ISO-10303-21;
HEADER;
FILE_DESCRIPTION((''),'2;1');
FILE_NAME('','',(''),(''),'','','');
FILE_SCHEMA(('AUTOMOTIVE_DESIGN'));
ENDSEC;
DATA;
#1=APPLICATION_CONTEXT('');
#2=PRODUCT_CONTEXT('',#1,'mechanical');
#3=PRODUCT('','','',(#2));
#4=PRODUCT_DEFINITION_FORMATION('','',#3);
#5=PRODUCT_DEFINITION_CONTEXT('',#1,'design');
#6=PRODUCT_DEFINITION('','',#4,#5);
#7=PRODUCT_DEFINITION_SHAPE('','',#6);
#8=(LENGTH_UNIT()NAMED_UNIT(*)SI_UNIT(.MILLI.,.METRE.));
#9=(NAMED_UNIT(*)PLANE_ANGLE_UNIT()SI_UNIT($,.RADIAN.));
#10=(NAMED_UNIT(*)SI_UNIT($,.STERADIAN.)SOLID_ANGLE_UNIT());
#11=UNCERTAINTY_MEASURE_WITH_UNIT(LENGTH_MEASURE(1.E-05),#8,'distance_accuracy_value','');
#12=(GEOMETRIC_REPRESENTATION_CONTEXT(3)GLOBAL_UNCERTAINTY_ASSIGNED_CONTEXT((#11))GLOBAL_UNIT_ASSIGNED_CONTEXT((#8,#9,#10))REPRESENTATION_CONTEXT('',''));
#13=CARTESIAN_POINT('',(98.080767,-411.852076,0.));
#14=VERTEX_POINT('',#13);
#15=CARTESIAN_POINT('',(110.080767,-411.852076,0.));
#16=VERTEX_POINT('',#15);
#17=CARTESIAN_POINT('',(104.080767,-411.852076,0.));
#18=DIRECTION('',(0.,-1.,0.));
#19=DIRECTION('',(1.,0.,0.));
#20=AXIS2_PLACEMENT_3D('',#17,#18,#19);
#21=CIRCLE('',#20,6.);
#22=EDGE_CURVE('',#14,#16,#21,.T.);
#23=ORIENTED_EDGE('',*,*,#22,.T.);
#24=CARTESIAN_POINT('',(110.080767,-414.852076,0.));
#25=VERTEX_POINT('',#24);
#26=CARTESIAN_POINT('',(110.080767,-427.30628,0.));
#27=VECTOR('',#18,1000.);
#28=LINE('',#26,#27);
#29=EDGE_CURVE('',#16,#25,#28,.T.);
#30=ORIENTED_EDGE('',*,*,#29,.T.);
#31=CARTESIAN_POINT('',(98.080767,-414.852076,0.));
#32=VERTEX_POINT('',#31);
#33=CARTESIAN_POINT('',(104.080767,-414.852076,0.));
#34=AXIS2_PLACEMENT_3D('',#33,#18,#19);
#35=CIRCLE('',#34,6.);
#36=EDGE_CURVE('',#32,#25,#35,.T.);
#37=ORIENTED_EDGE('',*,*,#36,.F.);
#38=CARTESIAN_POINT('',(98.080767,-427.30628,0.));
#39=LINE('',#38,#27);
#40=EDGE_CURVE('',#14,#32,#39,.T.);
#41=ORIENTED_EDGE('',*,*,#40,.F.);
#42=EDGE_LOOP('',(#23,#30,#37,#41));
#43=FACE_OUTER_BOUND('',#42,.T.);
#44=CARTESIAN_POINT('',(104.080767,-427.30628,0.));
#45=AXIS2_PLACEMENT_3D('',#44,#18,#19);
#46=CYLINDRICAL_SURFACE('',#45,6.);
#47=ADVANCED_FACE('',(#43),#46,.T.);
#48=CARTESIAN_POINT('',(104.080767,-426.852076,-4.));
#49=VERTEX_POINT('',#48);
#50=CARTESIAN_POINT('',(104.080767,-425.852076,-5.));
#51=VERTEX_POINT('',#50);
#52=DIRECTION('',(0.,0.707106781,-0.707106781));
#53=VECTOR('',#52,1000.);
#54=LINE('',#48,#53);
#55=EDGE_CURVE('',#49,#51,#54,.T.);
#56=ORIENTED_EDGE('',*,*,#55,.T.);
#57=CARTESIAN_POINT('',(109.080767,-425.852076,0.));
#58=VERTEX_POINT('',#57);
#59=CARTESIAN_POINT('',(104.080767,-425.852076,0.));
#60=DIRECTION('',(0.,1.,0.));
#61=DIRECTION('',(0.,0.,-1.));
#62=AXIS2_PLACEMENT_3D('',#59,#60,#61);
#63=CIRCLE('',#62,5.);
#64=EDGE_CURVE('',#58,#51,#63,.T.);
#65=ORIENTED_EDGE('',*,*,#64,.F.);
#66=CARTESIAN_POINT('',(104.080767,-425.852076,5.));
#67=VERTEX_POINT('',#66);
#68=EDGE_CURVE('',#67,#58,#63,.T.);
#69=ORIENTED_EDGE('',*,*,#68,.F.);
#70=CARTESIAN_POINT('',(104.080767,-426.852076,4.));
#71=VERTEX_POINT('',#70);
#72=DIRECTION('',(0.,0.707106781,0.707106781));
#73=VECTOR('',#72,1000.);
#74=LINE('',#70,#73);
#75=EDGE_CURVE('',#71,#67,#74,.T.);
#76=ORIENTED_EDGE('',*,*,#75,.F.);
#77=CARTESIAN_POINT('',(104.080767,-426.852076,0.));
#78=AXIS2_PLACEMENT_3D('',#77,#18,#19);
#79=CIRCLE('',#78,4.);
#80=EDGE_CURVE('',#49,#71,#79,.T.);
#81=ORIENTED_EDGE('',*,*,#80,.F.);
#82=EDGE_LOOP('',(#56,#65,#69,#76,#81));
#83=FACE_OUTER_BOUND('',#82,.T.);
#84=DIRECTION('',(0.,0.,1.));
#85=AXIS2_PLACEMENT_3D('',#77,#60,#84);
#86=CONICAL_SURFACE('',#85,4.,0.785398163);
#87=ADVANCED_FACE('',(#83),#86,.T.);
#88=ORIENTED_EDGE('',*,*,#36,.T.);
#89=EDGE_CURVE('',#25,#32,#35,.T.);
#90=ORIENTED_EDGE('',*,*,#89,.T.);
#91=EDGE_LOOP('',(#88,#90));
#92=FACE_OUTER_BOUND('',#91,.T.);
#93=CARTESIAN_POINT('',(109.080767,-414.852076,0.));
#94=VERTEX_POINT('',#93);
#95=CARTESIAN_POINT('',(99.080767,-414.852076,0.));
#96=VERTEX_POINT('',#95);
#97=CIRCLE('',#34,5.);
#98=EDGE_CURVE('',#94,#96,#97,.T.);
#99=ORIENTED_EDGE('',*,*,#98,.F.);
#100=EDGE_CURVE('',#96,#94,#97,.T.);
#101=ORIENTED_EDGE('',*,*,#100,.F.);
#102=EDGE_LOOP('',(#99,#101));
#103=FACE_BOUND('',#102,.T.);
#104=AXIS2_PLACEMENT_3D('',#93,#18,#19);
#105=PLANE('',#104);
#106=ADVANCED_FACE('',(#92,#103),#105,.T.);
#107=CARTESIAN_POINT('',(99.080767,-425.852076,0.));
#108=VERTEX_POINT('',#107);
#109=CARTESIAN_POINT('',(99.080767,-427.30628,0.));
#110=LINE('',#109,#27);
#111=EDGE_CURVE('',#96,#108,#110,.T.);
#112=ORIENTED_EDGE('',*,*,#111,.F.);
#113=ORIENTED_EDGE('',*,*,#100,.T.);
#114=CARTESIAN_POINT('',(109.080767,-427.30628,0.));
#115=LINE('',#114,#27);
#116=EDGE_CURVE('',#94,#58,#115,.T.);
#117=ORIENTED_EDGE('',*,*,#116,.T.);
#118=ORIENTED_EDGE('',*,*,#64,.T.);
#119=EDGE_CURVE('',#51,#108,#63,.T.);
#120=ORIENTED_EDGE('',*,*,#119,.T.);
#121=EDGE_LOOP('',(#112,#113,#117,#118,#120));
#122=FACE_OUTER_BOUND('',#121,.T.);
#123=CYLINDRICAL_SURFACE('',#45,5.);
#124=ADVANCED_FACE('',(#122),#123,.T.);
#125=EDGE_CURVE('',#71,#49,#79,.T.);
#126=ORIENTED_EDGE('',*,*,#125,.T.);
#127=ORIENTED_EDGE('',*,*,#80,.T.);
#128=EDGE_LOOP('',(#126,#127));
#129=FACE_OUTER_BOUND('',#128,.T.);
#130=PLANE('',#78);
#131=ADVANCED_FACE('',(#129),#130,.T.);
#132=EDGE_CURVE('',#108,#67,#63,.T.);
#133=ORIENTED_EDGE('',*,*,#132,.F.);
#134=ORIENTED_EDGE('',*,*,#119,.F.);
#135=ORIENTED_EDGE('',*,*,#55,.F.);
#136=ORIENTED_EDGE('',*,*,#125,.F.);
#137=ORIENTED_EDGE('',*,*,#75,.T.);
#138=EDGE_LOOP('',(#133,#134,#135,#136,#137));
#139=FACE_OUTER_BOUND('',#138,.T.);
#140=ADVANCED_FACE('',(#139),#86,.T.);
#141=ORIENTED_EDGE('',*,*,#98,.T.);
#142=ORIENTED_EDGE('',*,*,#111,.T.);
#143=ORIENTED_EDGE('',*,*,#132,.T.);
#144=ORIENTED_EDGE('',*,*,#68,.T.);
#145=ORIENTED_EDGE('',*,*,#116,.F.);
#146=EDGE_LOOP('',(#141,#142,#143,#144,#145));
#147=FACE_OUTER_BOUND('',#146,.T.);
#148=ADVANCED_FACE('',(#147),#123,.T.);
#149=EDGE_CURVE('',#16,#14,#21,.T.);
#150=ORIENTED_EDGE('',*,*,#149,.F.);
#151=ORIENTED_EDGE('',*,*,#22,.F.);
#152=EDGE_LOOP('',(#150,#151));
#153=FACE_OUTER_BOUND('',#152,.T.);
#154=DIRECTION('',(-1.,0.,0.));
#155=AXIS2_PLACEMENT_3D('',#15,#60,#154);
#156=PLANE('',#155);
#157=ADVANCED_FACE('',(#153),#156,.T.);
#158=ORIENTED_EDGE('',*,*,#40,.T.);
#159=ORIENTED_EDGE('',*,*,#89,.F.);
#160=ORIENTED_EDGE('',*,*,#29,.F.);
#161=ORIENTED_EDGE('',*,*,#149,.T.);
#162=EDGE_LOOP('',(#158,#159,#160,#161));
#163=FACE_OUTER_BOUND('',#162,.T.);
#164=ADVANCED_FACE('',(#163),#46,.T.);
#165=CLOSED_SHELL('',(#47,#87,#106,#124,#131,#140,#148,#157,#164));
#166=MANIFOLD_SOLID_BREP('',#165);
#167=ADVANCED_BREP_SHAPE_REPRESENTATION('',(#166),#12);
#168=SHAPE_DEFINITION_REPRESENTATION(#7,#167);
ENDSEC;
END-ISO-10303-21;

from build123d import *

# Parameters (mm, degrees)
CHAMFER1_SIZE = 1


with BuildPart() as part:
    # Sketch1 → Revolve1 (revolve)
    with BuildSketch(Plane.XY):
        Polygon((104.080767339, -426.85207641), (109.080767339, -426.85207641), (109.080767339, -414.85207641), (110.080767339, -414.85207641), (110.080767339, -411.85207641), (104.080767339, -411.85207641), align=None)
    revolve(axis=Axis((104.080767339, -427.306279578, 0), (0, 1, 0)))

    # Chamfer1
    chamfer1_edges = [part.edges().sort_by_distance(p)[0] for p in [
        (99.080767339, -426.85207641, 0),
    ]]
    chamfer(chamfer1_edges, length=CHAMFER1_SIZE)


solid = part.part
